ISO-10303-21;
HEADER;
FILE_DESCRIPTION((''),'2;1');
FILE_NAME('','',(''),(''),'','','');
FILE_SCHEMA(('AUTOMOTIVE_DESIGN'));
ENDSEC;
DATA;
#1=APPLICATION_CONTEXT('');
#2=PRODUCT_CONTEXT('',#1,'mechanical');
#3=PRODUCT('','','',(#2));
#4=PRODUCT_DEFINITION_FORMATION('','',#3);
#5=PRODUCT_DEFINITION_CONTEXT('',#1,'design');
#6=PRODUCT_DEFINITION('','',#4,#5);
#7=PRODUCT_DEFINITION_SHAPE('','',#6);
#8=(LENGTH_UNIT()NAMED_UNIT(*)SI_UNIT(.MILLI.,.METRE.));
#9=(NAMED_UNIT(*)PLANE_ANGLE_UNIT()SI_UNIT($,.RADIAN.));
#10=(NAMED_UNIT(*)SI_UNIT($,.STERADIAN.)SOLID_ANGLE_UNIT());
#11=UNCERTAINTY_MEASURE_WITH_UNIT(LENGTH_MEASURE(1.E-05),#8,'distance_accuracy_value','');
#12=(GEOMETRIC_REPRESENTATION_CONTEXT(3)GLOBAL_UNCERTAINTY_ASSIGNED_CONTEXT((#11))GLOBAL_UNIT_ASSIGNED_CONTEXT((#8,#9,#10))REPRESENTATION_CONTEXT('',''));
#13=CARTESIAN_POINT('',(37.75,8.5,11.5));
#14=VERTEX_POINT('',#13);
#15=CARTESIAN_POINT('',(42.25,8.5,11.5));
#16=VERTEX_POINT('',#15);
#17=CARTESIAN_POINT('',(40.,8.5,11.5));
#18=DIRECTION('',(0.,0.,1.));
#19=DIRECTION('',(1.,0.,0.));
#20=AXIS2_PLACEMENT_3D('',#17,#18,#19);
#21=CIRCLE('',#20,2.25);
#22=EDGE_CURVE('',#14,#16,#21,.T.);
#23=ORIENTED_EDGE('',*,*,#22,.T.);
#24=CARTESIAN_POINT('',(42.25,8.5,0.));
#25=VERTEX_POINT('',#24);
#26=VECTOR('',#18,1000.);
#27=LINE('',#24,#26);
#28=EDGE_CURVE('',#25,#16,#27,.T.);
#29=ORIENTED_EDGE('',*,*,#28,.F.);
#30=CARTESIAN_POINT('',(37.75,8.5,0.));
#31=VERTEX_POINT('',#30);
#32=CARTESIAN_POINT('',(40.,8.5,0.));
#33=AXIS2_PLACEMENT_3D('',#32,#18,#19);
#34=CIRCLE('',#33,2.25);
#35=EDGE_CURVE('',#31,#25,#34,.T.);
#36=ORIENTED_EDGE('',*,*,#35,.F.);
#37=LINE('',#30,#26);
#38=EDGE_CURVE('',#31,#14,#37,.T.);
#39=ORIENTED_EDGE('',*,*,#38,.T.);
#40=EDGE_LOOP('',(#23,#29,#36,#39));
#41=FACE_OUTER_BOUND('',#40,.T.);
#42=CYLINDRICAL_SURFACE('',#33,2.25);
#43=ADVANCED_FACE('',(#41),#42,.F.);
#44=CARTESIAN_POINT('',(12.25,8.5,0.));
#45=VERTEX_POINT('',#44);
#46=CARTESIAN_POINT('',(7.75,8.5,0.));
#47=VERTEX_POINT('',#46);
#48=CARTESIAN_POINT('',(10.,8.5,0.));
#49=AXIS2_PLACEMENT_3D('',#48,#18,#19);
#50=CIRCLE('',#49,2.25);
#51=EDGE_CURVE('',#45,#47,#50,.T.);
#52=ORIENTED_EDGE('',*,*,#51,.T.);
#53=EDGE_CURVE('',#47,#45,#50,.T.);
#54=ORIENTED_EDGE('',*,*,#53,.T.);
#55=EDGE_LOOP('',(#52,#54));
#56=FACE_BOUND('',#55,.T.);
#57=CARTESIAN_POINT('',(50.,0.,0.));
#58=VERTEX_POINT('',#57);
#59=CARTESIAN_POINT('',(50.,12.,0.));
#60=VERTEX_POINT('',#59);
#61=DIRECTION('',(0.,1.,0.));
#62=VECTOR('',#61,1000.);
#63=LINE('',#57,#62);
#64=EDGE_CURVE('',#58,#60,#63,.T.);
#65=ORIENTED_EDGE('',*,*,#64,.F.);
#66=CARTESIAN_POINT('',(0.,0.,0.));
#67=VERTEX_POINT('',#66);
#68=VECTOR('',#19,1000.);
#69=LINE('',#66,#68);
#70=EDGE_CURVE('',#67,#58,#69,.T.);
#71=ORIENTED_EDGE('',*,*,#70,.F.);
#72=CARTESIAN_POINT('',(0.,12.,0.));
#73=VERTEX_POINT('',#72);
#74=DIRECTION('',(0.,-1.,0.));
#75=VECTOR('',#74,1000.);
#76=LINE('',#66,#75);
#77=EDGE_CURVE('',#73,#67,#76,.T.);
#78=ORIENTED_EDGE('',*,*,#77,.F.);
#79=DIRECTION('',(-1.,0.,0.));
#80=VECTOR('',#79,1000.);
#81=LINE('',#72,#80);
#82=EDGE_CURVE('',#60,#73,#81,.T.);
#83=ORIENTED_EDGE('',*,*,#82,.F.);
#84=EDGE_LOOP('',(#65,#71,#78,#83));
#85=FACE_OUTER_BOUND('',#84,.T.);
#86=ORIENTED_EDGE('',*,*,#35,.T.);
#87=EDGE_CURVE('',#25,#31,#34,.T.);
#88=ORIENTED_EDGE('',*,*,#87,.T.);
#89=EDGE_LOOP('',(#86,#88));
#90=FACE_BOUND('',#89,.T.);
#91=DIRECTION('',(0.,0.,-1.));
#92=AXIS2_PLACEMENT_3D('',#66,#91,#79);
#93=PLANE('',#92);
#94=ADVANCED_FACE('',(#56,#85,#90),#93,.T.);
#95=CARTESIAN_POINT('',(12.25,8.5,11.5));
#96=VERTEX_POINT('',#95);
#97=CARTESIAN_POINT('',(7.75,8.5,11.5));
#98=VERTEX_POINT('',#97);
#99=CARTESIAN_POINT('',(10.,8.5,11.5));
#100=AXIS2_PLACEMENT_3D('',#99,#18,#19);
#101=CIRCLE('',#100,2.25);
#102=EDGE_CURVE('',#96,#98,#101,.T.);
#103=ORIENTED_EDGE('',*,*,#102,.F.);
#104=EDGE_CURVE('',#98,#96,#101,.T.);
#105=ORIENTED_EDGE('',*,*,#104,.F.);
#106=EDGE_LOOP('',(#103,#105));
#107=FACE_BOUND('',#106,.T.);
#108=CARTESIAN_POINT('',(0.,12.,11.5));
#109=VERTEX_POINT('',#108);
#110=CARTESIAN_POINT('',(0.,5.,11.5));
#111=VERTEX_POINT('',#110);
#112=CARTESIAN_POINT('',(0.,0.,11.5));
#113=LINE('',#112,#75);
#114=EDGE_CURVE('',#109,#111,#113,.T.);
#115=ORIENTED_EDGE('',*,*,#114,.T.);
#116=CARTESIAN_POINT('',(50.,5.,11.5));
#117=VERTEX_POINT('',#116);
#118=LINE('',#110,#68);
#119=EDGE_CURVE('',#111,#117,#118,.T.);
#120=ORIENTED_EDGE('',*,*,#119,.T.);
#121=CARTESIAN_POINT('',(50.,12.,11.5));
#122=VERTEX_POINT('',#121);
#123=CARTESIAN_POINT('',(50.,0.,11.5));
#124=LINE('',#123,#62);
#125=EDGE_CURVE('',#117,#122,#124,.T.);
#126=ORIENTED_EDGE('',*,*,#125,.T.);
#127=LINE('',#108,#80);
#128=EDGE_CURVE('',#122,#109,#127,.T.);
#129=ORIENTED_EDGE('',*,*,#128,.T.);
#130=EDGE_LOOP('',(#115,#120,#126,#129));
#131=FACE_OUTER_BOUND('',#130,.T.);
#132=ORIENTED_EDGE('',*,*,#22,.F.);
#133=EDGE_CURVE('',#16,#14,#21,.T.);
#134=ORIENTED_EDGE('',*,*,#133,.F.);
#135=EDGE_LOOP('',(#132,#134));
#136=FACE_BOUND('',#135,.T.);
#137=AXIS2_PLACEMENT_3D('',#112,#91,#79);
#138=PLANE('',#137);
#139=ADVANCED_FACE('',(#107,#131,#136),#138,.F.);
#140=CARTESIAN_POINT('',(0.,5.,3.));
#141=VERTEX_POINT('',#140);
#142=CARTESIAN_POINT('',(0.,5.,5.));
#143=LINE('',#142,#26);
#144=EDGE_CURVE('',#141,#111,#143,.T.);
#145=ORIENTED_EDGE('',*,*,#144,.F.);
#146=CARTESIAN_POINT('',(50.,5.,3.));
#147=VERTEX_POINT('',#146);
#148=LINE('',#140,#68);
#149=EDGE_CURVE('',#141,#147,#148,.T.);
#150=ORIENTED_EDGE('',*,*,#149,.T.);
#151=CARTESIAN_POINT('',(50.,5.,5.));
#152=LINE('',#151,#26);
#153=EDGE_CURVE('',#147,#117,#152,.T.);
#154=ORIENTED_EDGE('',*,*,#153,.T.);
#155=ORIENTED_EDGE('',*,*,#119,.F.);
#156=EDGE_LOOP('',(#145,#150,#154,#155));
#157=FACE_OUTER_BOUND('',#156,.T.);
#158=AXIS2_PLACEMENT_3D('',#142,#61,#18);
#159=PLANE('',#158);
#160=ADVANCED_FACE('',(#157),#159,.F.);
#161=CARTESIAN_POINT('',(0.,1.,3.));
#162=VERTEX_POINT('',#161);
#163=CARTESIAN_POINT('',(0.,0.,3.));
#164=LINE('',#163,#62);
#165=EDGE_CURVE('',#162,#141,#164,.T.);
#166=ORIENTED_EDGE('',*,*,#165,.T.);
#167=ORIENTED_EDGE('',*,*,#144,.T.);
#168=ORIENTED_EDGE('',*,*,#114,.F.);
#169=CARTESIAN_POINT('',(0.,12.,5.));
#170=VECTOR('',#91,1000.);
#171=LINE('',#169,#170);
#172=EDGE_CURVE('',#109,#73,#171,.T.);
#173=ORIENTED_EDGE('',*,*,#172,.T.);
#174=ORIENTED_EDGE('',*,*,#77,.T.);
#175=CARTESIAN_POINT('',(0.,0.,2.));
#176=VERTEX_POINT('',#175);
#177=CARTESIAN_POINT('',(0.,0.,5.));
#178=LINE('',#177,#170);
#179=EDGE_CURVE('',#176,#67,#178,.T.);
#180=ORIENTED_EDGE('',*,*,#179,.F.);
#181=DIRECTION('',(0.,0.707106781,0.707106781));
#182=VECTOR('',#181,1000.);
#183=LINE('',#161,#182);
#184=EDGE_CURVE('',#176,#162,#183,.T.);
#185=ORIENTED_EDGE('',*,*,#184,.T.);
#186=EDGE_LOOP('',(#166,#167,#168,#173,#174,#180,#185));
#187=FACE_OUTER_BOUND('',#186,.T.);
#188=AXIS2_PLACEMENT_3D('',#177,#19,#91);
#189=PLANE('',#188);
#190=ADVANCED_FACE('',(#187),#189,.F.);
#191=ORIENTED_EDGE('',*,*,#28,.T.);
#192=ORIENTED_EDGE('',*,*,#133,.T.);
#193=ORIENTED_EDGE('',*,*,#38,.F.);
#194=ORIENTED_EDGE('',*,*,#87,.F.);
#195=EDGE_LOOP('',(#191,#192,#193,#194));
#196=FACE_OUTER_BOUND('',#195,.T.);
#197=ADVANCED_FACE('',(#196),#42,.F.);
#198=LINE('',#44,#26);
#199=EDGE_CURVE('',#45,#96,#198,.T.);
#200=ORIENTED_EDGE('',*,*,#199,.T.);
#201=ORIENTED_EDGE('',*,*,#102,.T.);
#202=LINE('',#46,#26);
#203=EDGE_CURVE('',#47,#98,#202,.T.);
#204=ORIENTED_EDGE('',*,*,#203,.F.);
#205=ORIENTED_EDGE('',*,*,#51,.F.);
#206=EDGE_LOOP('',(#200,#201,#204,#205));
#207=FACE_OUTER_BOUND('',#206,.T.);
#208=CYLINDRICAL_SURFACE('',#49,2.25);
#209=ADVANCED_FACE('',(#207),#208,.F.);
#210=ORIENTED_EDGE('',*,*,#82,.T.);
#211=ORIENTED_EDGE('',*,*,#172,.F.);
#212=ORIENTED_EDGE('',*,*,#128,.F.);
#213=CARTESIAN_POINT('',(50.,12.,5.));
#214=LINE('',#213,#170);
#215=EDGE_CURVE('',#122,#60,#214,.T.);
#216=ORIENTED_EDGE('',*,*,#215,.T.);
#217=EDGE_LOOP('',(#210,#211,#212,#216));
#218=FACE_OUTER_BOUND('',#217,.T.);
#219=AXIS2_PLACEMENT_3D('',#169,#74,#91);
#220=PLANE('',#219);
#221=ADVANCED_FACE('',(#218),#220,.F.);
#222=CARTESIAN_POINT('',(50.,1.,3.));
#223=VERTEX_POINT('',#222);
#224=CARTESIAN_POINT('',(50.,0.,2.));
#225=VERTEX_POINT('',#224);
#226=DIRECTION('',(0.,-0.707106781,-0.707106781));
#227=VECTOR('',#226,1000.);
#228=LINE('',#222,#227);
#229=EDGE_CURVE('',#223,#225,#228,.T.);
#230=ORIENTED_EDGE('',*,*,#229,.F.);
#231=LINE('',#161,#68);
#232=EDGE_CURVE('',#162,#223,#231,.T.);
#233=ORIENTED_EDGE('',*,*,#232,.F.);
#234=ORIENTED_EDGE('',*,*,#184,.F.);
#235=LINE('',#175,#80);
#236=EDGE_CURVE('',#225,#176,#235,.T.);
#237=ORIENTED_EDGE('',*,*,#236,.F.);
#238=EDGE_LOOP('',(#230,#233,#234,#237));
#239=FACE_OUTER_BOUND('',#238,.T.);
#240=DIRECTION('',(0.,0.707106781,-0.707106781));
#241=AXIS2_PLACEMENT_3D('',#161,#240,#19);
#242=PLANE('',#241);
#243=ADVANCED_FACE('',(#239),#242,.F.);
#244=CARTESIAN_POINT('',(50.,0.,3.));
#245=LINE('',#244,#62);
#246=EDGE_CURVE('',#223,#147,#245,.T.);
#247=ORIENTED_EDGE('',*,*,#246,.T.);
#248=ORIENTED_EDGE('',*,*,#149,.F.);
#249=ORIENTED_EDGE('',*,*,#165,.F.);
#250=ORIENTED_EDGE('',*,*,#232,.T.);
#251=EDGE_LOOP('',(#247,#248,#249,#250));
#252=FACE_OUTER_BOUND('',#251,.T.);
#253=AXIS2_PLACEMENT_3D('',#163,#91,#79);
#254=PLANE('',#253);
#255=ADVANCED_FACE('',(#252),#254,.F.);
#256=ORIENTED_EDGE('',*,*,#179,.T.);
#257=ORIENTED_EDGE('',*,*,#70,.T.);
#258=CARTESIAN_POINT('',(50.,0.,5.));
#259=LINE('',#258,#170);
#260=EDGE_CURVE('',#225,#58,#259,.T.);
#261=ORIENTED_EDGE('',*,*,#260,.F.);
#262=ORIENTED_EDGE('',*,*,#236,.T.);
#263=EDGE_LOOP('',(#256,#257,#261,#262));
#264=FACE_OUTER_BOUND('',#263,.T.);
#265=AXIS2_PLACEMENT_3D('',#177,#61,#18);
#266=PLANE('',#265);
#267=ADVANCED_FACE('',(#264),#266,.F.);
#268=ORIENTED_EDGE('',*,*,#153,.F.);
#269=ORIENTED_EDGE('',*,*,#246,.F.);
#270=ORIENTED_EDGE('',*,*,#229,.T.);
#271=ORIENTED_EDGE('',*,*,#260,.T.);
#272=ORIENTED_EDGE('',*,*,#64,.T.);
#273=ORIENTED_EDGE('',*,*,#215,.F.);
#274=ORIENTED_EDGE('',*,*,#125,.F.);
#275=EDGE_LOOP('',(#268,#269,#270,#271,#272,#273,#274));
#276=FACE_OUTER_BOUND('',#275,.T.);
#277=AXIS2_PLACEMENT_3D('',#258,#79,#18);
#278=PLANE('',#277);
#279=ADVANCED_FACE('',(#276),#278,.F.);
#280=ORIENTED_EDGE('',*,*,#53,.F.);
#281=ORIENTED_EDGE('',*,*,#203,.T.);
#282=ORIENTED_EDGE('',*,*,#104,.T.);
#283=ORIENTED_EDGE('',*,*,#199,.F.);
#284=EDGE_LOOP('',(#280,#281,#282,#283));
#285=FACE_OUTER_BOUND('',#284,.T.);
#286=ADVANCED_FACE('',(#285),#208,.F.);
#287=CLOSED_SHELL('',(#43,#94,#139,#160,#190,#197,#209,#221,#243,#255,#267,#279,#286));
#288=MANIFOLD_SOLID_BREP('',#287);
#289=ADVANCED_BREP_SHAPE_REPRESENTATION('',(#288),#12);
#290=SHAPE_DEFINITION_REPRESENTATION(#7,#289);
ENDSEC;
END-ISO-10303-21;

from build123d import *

# Parameters (mm, degrees)
SKETCH1_W           = 50
SKETCH1_H           = 12
BOSS_EXTRUDE1_DEPTH = 5
SKETCH2_R           = 2.25
CUT_EXTRUDE1_DEPTH  = 52.662365412
SKETCH3_W           = 2
SKETCH3_H           = 5
CUT_EXTRUDE2_DEPTH  = 52.662365412
CHAMFER1_SIZE       = 1
MOVE_FACE1_BY       = 6.5


with BuildPart() as part:
    # Sketch1 → Boss-Extrude1 (new body)
    with BuildSketch(Plane.XY):
        with Locations((25, 6)):
            Rectangle(SKETCH1_W, SKETCH1_H)
    extrude(amount=BOSS_EXTRUDE1_DEPTH)

    # Sketch2 → Cut-Extrude1 (cut, through all)
    with BuildSketch(Plane.XY.offset(5)):
        with Locations((10, 8.5)):
            Circle(SKETCH2_R)
        with Locations((40, 8.5)):
            Circle(SKETCH2_R)
    extrude(amount=-CUT_EXTRUDE1_DEPTH, mode=Mode.SUBTRACT)

    # Sketch3 → Cut-Extrude2 (cut, through all)
    with BuildSketch(Plane(origin=(50, 0, 0), x_dir=(0, 0, -1), z_dir=(1, 0, 0))):
        with Locations((-4, 2.5)):
            Rectangle(SKETCH3_W, SKETCH3_H)
    extrude(amount=-CUT_EXTRUDE2_DEPTH, mode=Mode.SUBTRACT)

    # Chamfer1
    chamfer1_edges = [part.edges().sort_by_distance(p)[0] for p in [
        (25, 0, 3),
    ]]
    chamfer(chamfer1_edges, length=CHAMFER1_SIZE)

    # Move Face1: a face moved outward by 6.5
    extrude(part.faces().sort_by_distance((25, 8.5, 5))[0], amount=MOVE_FACE1_BY, dir=(0, 0, 1))


solid = part.part
